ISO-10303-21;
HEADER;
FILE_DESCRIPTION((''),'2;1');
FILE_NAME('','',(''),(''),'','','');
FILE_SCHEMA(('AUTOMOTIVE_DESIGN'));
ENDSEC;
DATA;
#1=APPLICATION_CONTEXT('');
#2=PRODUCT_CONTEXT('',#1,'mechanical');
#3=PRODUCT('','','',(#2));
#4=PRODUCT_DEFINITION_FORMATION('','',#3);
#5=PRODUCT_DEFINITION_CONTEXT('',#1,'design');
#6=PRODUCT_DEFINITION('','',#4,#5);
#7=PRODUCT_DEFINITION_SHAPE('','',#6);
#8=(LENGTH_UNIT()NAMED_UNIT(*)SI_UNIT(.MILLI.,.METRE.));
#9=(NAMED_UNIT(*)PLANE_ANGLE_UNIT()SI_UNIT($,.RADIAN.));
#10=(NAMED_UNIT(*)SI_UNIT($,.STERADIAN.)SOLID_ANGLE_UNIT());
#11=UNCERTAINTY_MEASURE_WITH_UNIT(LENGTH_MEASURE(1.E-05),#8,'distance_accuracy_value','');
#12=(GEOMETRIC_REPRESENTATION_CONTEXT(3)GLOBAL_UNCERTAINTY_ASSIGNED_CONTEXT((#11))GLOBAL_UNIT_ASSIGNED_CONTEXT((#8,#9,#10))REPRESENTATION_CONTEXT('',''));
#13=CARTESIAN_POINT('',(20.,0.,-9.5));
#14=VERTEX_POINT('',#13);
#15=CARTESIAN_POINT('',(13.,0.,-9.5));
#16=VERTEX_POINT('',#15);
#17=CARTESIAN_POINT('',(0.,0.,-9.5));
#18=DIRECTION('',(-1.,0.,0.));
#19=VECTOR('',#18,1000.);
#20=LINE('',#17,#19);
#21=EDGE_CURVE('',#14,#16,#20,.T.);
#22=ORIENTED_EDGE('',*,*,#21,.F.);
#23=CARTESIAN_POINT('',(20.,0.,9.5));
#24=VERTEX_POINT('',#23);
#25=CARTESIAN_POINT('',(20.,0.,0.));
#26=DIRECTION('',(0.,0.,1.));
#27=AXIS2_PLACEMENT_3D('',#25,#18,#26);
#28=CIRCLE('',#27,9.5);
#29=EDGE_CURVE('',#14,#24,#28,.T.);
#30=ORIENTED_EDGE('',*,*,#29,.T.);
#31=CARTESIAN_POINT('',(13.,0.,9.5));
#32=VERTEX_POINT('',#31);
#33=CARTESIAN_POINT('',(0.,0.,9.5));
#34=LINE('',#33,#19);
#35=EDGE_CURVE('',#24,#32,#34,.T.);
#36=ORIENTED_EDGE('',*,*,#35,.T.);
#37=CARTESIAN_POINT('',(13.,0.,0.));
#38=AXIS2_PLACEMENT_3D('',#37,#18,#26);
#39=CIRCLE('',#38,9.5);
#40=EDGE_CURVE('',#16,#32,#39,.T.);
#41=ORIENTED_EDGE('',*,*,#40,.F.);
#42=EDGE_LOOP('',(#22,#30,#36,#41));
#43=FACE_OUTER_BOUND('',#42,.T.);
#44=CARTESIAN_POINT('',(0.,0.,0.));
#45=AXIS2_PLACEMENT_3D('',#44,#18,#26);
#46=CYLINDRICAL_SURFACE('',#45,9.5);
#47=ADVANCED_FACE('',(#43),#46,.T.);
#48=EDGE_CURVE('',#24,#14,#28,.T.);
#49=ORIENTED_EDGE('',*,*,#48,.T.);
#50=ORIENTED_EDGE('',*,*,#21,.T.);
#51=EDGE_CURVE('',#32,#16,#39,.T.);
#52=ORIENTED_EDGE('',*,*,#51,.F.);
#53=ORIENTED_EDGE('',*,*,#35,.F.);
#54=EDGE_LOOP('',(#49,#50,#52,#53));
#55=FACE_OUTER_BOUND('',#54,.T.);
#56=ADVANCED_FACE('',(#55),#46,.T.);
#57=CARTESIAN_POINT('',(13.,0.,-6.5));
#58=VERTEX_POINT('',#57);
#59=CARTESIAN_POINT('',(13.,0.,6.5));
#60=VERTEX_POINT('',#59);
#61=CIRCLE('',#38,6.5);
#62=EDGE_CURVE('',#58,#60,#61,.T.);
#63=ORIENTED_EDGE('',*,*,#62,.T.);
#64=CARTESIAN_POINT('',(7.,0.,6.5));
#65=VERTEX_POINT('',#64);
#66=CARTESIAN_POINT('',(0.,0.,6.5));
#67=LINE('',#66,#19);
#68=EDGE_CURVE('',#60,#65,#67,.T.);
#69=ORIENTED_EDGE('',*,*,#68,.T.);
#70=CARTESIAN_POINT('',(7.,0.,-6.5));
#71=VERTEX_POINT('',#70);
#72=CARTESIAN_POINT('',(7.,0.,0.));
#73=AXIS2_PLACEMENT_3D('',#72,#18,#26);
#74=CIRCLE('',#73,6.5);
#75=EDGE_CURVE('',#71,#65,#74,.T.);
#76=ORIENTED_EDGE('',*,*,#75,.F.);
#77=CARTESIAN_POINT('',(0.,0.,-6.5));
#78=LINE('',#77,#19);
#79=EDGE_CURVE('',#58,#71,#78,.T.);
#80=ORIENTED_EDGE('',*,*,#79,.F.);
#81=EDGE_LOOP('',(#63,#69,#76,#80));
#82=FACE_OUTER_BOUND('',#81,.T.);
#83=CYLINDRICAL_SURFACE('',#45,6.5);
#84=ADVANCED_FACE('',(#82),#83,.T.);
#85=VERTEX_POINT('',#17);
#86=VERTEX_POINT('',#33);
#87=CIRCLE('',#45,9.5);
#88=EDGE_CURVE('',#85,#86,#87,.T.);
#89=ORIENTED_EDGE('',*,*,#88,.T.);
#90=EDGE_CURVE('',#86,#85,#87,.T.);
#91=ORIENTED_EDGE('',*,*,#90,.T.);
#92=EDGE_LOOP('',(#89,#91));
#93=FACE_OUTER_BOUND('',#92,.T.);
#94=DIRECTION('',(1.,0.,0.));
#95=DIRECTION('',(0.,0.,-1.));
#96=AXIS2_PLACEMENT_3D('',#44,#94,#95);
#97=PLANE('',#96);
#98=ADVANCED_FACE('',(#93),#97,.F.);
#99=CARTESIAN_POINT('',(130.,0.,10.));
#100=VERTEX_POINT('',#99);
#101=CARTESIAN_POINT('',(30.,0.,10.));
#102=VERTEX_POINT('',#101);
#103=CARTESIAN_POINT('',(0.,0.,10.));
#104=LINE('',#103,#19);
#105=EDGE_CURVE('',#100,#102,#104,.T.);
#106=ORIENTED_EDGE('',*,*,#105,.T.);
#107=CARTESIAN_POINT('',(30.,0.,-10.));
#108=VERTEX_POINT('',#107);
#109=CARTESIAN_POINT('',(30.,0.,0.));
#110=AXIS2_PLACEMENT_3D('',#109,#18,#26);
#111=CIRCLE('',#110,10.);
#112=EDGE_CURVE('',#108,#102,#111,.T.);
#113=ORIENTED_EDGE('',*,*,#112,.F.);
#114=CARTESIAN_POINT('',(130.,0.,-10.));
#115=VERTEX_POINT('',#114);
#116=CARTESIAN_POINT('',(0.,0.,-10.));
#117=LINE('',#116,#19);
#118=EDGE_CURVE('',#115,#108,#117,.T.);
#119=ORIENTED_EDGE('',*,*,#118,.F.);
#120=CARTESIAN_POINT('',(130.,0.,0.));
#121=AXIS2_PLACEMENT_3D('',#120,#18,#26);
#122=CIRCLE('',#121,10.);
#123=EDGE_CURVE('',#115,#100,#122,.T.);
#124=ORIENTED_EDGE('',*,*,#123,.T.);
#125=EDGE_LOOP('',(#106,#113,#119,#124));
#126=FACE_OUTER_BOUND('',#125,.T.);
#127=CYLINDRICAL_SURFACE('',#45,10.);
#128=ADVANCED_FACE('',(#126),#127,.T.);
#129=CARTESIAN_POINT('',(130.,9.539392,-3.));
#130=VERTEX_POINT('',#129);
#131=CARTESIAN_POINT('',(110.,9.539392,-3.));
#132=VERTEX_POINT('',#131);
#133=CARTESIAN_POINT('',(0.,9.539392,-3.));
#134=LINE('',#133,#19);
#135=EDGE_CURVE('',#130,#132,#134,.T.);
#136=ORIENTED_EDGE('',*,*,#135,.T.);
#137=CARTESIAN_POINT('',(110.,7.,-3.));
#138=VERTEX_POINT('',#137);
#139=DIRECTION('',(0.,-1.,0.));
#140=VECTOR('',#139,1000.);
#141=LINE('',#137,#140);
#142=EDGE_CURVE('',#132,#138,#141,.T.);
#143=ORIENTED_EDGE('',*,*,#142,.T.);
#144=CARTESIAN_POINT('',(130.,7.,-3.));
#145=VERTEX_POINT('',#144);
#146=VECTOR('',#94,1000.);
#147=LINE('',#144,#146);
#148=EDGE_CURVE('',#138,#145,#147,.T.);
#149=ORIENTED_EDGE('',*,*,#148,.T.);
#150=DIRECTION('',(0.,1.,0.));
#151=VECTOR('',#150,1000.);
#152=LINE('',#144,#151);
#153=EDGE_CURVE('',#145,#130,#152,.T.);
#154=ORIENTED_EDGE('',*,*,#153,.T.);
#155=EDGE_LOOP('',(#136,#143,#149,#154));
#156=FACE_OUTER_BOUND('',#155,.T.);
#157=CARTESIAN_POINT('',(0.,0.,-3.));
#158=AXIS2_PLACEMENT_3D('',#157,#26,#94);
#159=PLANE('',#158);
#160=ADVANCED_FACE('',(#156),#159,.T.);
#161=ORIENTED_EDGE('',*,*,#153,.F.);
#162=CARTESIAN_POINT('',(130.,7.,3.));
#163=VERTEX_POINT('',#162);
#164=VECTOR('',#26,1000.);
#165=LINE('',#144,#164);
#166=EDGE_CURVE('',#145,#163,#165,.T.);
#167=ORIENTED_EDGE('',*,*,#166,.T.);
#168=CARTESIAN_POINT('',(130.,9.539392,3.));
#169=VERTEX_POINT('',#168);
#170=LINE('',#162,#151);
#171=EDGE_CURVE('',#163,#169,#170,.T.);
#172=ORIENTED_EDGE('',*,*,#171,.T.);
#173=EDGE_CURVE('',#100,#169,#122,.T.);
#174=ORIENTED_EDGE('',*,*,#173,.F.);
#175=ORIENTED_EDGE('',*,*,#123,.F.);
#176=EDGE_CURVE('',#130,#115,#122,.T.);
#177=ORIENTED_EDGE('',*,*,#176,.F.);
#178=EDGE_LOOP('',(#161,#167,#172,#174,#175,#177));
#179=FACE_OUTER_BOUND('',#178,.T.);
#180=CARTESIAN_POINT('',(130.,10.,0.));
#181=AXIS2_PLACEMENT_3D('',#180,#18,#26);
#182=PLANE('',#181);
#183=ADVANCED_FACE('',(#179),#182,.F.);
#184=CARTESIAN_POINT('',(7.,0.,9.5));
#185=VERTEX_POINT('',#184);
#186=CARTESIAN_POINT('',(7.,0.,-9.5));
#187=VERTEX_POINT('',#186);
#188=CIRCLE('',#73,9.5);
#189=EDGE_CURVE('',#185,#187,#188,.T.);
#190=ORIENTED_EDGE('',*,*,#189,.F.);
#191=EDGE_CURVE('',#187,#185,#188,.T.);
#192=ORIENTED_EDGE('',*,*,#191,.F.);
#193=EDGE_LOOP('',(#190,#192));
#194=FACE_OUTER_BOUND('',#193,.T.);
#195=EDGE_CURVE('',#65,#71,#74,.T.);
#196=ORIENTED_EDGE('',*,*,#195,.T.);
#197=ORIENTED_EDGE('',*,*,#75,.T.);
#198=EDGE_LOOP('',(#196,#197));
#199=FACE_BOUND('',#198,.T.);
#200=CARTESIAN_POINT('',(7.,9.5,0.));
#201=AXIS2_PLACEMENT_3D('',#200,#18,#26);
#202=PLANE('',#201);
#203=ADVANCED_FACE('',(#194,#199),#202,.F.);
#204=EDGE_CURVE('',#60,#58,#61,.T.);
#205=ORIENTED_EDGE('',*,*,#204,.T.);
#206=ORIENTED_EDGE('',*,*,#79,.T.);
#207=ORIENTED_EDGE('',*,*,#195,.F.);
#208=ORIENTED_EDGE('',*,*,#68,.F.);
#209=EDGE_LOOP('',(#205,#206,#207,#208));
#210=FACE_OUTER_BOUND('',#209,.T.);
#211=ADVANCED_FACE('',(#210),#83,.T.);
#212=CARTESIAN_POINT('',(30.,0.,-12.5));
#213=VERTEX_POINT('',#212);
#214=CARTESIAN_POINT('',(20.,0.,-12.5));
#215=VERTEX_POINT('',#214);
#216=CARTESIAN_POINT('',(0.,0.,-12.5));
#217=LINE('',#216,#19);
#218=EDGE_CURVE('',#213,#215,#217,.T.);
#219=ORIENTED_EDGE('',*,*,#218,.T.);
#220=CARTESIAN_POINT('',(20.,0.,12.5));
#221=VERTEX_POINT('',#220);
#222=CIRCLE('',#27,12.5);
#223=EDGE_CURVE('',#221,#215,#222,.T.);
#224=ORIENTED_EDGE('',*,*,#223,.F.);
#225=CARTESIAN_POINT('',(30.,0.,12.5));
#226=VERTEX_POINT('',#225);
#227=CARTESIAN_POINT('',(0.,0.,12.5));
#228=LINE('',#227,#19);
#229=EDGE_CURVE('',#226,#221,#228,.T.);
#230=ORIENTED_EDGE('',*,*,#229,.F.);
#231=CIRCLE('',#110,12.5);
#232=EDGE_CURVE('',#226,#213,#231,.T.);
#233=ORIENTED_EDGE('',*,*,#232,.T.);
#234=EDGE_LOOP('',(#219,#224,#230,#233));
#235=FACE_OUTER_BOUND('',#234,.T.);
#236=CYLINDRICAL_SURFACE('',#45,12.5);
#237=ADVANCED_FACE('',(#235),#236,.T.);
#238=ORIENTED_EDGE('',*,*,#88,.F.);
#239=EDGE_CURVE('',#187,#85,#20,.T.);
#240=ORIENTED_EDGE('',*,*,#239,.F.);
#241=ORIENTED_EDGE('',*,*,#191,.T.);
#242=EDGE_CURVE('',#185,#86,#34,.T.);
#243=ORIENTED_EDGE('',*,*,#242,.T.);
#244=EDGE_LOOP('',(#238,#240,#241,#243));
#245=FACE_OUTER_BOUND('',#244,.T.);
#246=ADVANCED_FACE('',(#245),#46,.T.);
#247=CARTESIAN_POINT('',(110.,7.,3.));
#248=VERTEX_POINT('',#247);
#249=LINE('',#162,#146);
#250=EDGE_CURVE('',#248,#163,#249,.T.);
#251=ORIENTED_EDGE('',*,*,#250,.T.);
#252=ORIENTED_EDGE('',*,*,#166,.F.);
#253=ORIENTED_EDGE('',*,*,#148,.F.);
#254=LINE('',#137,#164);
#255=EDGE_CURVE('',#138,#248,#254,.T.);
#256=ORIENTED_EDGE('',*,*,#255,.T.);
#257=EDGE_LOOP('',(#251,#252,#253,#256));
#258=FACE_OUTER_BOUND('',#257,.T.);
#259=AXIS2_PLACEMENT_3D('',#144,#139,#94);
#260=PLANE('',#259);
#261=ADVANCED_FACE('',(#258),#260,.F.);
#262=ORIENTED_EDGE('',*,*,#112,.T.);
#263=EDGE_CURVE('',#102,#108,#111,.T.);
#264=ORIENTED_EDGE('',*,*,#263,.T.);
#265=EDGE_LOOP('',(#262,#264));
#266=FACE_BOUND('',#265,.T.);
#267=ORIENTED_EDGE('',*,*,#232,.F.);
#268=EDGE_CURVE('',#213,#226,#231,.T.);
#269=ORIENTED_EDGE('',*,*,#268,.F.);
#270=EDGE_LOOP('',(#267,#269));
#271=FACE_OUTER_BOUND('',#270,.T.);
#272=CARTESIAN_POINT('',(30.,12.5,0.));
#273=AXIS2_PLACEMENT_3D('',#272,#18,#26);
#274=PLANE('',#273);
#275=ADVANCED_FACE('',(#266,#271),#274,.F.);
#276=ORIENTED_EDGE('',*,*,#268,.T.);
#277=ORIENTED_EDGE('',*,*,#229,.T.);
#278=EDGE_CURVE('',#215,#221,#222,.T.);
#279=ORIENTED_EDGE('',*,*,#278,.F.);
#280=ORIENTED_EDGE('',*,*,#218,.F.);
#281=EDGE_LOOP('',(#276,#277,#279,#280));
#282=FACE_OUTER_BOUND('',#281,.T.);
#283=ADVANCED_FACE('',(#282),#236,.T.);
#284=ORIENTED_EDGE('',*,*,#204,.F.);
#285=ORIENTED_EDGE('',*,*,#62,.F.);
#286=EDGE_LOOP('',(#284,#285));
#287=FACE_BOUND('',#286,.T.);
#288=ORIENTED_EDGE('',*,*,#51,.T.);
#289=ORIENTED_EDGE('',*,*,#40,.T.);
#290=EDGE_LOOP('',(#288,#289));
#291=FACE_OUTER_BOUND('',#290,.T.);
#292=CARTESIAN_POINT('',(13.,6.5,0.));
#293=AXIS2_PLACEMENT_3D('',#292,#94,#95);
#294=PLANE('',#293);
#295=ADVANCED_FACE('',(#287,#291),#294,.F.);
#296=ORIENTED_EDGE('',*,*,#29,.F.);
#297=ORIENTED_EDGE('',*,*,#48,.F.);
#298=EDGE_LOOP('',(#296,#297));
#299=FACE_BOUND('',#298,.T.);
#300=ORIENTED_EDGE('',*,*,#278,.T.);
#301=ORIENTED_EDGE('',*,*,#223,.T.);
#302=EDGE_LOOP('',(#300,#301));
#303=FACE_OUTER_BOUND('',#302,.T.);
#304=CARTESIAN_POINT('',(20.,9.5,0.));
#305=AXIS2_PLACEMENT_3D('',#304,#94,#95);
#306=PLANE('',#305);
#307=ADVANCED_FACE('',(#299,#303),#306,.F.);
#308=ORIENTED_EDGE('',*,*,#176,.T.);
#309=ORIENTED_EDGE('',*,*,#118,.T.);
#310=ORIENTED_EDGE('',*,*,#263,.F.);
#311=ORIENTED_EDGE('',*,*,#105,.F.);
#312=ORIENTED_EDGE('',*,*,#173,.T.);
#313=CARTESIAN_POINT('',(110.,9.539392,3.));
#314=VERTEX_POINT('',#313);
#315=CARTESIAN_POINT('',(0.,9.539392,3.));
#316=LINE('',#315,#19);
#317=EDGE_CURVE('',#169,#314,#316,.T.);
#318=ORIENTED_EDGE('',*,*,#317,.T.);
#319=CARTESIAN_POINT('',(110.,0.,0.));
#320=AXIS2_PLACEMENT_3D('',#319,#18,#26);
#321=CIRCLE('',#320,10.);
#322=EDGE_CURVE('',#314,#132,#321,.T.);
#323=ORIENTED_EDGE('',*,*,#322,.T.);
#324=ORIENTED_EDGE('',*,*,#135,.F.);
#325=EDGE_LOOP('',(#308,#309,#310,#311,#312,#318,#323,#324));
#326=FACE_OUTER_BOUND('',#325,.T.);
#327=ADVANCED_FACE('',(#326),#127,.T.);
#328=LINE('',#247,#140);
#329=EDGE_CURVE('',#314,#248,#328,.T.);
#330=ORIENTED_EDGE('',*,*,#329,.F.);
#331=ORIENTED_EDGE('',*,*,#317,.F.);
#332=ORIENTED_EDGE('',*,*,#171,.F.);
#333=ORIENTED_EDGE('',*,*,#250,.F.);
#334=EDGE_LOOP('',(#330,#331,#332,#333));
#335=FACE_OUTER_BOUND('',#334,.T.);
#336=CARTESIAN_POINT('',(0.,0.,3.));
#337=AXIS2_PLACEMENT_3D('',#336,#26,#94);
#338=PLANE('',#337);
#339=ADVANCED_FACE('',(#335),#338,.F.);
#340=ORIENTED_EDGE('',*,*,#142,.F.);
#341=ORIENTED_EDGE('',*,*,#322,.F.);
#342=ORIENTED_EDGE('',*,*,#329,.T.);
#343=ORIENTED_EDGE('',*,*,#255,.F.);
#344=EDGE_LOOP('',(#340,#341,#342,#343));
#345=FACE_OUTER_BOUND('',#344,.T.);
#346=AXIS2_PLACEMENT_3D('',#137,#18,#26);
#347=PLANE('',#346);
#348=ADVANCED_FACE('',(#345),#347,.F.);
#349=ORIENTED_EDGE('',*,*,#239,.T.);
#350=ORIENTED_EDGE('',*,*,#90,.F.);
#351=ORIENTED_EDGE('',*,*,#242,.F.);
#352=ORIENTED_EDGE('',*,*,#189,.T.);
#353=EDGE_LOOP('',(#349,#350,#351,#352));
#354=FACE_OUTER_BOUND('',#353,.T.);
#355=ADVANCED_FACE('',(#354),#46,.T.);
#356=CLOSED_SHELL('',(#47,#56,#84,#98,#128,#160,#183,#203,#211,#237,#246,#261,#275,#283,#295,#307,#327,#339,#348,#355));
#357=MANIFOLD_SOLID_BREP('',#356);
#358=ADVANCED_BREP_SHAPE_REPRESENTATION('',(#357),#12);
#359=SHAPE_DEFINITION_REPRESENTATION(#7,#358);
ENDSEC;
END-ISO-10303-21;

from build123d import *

# Parameters (mm, degrees)
KEYWAY_SKETCH_W  = 20
KEYWAY_SKETCH_H  = 5
KEYWAY_CUT_DEPTH = 3


with BuildPart() as part:
    # Shaft Profile Sketch → Stepped Shaft Body (revolve)
    with BuildSketch(Plane.XY, mode=Mode.PRIVATE) as stepped_shaft_body_sk:
        Polygon((0, 0), (0, 9.5), (7, 9.5), (7, 6.5), (13, 6.5), (13, 9.5), (20, 9.5), (20, 12.5), (30, 12.5), (30, 10), (130, 10), (130, 0), align=None)
    revolve(stepped_shaft_body_sk.sketch.rotate(Axis((0, 0, 0), (1, 0, 0)), 90), axis=Axis((0, 0, 0), (1, 0, 0)))

    # Keyway Sketch → Keyway Cut (cut, symmetric)
    with BuildSketch(Plane.XY):
        with Locations((120, 9.5)):
            Rectangle(KEYWAY_SKETCH_W, KEYWAY_SKETCH_H)
    extrude(amount=KEYWAY_CUT_DEPTH, both=True, mode=Mode.SUBTRACT)


solid = part.part
